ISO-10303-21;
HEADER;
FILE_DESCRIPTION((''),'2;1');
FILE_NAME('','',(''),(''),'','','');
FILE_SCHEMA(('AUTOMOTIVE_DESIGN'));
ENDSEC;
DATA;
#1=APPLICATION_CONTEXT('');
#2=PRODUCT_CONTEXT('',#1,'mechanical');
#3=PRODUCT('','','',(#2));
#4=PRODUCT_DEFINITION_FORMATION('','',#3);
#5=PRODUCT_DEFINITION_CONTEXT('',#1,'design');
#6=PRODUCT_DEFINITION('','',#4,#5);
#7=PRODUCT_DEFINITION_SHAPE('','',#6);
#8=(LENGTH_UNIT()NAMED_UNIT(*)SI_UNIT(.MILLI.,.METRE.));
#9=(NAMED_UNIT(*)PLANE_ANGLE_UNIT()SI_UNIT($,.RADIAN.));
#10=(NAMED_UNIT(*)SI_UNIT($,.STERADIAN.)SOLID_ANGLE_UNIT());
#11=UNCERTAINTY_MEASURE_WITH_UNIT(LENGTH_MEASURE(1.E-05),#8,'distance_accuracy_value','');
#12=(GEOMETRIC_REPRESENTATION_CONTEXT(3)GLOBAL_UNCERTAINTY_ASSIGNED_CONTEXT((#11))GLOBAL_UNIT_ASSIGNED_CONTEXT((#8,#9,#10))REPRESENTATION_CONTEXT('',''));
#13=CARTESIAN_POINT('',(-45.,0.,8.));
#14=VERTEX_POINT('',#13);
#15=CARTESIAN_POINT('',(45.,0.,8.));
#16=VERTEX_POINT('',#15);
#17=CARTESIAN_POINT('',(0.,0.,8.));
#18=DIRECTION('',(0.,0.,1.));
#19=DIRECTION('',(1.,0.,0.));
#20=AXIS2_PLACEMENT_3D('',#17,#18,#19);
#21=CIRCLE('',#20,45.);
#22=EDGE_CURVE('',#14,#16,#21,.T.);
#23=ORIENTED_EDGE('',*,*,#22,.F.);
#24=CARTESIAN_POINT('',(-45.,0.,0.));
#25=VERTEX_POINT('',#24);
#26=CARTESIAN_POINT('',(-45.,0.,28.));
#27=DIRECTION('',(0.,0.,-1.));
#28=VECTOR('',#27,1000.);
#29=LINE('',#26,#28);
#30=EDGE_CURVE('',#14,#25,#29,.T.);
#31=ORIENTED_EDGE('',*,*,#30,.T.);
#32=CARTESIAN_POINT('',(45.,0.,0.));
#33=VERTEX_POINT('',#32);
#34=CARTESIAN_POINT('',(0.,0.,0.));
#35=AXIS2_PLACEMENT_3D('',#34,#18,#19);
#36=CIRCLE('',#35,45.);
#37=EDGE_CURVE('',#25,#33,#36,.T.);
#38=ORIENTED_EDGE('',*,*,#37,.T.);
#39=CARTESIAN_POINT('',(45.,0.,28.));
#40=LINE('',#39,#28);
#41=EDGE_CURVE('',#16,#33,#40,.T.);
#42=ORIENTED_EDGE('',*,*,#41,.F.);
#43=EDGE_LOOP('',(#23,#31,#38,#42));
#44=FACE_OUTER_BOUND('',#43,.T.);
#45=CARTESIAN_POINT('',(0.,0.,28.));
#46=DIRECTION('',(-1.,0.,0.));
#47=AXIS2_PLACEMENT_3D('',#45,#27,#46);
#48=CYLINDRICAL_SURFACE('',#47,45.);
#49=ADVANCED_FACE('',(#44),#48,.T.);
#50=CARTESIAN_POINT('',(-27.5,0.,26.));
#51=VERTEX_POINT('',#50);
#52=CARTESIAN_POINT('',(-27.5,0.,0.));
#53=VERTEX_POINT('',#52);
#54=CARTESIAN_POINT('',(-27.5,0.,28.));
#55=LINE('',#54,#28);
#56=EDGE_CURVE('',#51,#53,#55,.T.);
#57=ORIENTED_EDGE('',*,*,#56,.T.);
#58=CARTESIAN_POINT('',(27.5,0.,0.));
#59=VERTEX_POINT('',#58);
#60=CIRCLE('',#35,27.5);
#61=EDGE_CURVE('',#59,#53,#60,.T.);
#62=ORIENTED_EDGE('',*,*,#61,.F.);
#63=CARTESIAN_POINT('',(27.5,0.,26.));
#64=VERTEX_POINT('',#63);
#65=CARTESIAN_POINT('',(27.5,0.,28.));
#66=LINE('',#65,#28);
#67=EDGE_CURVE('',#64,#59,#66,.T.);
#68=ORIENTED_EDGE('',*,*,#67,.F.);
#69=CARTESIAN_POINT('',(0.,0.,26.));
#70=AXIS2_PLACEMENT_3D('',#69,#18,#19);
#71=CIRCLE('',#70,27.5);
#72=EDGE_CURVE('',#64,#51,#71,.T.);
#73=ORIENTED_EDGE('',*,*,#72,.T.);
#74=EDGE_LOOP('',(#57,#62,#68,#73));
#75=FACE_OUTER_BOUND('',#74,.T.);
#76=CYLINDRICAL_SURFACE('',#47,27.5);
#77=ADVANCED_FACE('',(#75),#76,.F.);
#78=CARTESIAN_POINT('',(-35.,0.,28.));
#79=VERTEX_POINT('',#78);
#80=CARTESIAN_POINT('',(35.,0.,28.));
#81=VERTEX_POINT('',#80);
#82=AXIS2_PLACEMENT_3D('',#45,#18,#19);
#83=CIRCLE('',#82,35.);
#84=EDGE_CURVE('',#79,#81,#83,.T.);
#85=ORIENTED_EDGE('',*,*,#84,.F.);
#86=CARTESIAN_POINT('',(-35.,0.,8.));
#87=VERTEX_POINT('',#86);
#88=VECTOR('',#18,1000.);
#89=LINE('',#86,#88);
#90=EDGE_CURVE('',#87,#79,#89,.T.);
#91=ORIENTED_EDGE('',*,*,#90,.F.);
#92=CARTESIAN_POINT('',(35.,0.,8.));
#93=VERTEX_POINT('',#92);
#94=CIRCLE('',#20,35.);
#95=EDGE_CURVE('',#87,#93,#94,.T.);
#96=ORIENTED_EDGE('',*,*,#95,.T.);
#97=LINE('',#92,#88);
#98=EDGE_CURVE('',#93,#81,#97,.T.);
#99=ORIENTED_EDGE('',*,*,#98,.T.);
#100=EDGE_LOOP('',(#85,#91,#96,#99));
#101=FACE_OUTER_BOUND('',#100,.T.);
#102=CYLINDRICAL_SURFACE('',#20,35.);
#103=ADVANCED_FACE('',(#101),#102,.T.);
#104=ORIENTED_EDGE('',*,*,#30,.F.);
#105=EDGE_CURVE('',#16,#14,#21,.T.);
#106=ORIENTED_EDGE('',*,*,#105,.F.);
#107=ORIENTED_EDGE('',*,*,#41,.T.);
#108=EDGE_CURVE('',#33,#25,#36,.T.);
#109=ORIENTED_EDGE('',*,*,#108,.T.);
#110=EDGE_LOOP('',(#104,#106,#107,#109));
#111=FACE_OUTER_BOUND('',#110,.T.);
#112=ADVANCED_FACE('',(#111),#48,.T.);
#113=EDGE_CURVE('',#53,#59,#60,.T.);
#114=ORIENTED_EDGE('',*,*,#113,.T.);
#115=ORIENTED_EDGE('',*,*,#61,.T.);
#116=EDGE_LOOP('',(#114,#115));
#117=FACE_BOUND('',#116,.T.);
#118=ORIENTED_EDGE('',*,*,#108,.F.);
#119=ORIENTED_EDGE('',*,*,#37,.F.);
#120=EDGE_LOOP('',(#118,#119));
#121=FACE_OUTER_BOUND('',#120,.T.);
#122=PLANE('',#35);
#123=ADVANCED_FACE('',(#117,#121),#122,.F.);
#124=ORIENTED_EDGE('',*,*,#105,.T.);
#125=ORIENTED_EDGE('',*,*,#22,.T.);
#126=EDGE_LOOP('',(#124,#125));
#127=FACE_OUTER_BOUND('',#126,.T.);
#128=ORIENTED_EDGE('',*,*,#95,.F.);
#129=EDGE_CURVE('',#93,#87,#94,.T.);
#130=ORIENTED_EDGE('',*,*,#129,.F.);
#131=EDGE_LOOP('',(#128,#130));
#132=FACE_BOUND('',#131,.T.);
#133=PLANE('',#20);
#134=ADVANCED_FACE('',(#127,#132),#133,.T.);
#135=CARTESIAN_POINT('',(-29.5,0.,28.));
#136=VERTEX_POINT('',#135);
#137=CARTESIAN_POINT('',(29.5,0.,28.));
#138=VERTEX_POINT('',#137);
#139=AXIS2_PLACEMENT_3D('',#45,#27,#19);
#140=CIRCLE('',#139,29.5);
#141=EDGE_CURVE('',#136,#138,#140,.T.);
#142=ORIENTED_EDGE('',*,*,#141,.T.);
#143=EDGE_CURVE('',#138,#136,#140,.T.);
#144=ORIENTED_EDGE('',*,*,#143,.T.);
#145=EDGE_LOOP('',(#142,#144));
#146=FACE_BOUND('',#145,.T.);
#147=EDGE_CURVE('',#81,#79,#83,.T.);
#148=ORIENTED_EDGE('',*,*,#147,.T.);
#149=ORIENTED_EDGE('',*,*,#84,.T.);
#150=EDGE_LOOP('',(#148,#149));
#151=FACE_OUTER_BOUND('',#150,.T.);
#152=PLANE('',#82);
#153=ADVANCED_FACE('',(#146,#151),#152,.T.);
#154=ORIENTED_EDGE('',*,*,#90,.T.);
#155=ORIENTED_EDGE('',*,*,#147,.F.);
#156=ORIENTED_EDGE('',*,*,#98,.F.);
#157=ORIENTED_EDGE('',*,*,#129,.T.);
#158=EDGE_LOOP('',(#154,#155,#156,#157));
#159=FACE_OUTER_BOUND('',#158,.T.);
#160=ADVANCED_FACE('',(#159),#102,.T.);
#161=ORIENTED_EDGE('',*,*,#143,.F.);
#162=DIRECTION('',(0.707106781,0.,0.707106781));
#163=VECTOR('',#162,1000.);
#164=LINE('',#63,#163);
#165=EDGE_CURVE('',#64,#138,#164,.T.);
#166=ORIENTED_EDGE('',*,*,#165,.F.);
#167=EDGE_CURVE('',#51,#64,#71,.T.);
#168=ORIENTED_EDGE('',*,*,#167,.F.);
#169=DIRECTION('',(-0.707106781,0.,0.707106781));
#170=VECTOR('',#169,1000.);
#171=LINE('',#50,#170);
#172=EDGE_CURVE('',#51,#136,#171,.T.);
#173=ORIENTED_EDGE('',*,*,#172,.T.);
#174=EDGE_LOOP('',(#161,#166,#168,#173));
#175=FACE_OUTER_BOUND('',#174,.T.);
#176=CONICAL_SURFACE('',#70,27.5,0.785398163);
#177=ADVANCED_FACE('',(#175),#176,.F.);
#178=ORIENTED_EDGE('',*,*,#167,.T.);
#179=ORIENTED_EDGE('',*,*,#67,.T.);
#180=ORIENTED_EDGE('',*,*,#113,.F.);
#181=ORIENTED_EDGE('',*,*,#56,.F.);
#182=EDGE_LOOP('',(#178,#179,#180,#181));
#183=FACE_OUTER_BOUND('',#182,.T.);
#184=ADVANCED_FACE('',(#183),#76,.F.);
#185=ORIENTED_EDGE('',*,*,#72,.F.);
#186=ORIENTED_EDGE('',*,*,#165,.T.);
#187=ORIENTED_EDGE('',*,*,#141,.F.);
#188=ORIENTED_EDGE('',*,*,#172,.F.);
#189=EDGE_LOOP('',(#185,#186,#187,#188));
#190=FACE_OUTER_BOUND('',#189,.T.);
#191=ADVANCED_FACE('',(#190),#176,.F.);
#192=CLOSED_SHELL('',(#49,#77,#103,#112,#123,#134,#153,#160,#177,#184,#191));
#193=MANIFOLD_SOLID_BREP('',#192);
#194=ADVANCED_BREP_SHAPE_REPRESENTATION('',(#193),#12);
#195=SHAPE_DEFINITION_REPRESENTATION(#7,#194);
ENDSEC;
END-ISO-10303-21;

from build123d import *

# Parameters (mm, degrees)
SKETCH1_R           = 45
SKETCH1_R_2         = 27.5
BOSS_EXTRUDE1_DEPTH = 28
CUT_EXTRUDE1_START  = -20
SKETCH2_R           = 45
SKETCH2_R_2         = 35
CUT_EXTRUDE1_DEPTH  = 20
CHAMFER1_SIZE       = 2


with BuildPart() as part:
    # Sketch1 → Boss-Extrude1 (new body)
    with BuildSketch(Plane.XY):
        Circle(SKETCH1_R)
        Circle(SKETCH1_R_2, mode=Mode.SUBTRACT)
    extrude(amount=BOSS_EXTRUDE1_DEPTH)

    # Sketch2 → Cut-Extrude1 (cut)
    with BuildSketch(Plane.XY.offset(28).offset(CUT_EXTRUDE1_START)):
        Circle(SKETCH2_R)
        Circle(SKETCH2_R_2, mode=Mode.SUBTRACT)
    extrude(amount=CUT_EXTRUDE1_DEPTH, mode=Mode.SUBTRACT)

    # Chamfer1
    chamfer1_edges = [part.edges().sort_by_distance(p)[0] for p in [
        (-27.5, 0, 28),
    ]]
    chamfer(chamfer1_edges, length=CHAMFER1_SIZE)


solid = part.part
